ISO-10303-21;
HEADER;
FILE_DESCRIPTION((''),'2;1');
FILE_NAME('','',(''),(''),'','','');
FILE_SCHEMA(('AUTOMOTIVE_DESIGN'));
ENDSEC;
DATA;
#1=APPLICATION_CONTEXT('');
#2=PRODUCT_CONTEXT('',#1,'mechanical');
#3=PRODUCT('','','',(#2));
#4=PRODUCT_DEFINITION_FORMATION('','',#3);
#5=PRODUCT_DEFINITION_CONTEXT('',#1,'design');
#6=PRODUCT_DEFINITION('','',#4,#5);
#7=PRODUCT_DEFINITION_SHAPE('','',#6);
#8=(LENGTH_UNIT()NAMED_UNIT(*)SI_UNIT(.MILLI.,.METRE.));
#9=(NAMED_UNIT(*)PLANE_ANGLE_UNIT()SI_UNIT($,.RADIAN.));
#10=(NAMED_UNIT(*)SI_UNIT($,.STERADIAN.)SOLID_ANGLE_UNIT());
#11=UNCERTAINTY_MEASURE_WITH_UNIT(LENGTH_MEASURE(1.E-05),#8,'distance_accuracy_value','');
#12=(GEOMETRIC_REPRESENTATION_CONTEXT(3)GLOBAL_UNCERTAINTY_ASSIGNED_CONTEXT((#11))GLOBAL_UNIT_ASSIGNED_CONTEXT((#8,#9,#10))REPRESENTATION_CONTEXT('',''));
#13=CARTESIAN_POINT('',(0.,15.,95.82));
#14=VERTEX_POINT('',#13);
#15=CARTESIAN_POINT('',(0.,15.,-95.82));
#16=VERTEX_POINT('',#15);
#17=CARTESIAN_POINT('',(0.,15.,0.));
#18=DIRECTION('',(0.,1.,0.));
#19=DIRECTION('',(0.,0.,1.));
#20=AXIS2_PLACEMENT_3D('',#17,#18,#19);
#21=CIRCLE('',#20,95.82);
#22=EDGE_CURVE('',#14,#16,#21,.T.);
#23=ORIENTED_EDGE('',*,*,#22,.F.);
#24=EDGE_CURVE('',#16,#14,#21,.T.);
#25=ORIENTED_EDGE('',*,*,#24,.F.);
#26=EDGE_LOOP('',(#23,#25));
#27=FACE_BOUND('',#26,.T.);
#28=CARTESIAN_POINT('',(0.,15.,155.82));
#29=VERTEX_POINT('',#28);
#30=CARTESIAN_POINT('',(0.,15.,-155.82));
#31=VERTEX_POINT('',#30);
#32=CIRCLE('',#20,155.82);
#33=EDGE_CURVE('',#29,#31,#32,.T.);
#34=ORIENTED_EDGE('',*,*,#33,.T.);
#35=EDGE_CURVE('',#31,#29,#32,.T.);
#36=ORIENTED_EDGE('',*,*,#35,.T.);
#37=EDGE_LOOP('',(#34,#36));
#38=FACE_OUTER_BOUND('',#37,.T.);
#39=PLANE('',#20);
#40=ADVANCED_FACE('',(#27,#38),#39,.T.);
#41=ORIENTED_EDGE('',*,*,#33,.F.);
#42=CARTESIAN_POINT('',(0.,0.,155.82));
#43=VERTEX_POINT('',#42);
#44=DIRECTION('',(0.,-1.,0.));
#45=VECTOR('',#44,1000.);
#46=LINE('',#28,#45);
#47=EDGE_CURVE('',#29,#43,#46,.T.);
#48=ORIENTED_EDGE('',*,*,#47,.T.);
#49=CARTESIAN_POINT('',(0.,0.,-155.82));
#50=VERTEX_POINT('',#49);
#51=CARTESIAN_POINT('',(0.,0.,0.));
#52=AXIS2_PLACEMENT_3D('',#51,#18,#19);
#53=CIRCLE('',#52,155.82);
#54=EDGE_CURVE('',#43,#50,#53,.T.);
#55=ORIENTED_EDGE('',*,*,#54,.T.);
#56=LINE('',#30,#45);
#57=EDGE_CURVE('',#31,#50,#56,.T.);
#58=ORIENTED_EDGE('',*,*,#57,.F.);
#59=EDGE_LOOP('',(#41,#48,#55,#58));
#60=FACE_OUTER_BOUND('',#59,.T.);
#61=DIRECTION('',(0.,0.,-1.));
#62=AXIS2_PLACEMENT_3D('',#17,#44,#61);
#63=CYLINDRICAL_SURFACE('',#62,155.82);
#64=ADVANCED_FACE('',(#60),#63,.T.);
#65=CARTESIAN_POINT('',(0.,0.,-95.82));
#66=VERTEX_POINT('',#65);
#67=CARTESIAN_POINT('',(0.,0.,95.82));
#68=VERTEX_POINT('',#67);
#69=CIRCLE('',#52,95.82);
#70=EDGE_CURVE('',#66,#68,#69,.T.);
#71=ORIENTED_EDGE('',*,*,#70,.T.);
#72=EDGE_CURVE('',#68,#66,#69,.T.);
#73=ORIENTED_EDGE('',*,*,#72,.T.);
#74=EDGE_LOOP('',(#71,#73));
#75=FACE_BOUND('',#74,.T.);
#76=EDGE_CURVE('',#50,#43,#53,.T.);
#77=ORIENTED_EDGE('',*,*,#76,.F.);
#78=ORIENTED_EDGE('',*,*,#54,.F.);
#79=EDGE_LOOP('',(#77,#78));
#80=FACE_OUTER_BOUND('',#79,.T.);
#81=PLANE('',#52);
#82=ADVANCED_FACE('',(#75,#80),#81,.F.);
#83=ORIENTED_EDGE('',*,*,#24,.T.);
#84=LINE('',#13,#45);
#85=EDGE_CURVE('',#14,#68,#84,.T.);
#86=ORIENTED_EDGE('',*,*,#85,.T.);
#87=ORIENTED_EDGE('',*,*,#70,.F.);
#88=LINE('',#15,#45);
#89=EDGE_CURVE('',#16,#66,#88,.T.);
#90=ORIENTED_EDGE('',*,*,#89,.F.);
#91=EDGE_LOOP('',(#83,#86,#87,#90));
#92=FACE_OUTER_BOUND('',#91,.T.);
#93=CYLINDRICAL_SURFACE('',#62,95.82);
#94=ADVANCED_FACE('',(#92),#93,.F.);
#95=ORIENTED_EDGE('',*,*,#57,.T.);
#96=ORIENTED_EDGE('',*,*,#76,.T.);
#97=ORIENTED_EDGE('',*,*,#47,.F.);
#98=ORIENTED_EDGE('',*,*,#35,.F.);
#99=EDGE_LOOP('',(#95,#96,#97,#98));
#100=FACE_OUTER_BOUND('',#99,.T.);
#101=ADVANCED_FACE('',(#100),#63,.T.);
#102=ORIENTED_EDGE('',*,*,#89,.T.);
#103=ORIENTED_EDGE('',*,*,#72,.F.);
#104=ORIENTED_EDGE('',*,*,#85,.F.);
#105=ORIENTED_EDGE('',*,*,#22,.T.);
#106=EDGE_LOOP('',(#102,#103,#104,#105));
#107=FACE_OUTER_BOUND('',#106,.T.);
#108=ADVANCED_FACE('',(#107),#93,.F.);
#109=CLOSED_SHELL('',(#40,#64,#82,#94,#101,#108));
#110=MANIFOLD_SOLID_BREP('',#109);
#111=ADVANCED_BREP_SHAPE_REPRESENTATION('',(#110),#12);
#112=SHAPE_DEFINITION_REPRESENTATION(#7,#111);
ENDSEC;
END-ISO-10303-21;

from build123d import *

# Parameters (mm, degrees)
SKETCH_1_R      = 155.82
SKETCH_1_R_2    = 95.82
EXTRUDE_1_DEPTH = 15


with BuildPart() as part:
    # 草图1 → 凸台-拉伸1 (new body)
    with BuildSketch(Plane(origin=(0, 0, 0), x_dir=(1, 0, 0), z_dir=(0, 1, 0))):
        with Locations(Location((0, 0, 0), (0, 0, 270))):
            Circle(SKETCH_1_R)
        with Locations(Location((0, 0, 0), (0, 0, 270))):
            Circle(SKETCH_1_R_2, mode=Mode.SUBTRACT)
    extrude(amount=EXTRUDE_1_DEPTH)


solid = part.part
